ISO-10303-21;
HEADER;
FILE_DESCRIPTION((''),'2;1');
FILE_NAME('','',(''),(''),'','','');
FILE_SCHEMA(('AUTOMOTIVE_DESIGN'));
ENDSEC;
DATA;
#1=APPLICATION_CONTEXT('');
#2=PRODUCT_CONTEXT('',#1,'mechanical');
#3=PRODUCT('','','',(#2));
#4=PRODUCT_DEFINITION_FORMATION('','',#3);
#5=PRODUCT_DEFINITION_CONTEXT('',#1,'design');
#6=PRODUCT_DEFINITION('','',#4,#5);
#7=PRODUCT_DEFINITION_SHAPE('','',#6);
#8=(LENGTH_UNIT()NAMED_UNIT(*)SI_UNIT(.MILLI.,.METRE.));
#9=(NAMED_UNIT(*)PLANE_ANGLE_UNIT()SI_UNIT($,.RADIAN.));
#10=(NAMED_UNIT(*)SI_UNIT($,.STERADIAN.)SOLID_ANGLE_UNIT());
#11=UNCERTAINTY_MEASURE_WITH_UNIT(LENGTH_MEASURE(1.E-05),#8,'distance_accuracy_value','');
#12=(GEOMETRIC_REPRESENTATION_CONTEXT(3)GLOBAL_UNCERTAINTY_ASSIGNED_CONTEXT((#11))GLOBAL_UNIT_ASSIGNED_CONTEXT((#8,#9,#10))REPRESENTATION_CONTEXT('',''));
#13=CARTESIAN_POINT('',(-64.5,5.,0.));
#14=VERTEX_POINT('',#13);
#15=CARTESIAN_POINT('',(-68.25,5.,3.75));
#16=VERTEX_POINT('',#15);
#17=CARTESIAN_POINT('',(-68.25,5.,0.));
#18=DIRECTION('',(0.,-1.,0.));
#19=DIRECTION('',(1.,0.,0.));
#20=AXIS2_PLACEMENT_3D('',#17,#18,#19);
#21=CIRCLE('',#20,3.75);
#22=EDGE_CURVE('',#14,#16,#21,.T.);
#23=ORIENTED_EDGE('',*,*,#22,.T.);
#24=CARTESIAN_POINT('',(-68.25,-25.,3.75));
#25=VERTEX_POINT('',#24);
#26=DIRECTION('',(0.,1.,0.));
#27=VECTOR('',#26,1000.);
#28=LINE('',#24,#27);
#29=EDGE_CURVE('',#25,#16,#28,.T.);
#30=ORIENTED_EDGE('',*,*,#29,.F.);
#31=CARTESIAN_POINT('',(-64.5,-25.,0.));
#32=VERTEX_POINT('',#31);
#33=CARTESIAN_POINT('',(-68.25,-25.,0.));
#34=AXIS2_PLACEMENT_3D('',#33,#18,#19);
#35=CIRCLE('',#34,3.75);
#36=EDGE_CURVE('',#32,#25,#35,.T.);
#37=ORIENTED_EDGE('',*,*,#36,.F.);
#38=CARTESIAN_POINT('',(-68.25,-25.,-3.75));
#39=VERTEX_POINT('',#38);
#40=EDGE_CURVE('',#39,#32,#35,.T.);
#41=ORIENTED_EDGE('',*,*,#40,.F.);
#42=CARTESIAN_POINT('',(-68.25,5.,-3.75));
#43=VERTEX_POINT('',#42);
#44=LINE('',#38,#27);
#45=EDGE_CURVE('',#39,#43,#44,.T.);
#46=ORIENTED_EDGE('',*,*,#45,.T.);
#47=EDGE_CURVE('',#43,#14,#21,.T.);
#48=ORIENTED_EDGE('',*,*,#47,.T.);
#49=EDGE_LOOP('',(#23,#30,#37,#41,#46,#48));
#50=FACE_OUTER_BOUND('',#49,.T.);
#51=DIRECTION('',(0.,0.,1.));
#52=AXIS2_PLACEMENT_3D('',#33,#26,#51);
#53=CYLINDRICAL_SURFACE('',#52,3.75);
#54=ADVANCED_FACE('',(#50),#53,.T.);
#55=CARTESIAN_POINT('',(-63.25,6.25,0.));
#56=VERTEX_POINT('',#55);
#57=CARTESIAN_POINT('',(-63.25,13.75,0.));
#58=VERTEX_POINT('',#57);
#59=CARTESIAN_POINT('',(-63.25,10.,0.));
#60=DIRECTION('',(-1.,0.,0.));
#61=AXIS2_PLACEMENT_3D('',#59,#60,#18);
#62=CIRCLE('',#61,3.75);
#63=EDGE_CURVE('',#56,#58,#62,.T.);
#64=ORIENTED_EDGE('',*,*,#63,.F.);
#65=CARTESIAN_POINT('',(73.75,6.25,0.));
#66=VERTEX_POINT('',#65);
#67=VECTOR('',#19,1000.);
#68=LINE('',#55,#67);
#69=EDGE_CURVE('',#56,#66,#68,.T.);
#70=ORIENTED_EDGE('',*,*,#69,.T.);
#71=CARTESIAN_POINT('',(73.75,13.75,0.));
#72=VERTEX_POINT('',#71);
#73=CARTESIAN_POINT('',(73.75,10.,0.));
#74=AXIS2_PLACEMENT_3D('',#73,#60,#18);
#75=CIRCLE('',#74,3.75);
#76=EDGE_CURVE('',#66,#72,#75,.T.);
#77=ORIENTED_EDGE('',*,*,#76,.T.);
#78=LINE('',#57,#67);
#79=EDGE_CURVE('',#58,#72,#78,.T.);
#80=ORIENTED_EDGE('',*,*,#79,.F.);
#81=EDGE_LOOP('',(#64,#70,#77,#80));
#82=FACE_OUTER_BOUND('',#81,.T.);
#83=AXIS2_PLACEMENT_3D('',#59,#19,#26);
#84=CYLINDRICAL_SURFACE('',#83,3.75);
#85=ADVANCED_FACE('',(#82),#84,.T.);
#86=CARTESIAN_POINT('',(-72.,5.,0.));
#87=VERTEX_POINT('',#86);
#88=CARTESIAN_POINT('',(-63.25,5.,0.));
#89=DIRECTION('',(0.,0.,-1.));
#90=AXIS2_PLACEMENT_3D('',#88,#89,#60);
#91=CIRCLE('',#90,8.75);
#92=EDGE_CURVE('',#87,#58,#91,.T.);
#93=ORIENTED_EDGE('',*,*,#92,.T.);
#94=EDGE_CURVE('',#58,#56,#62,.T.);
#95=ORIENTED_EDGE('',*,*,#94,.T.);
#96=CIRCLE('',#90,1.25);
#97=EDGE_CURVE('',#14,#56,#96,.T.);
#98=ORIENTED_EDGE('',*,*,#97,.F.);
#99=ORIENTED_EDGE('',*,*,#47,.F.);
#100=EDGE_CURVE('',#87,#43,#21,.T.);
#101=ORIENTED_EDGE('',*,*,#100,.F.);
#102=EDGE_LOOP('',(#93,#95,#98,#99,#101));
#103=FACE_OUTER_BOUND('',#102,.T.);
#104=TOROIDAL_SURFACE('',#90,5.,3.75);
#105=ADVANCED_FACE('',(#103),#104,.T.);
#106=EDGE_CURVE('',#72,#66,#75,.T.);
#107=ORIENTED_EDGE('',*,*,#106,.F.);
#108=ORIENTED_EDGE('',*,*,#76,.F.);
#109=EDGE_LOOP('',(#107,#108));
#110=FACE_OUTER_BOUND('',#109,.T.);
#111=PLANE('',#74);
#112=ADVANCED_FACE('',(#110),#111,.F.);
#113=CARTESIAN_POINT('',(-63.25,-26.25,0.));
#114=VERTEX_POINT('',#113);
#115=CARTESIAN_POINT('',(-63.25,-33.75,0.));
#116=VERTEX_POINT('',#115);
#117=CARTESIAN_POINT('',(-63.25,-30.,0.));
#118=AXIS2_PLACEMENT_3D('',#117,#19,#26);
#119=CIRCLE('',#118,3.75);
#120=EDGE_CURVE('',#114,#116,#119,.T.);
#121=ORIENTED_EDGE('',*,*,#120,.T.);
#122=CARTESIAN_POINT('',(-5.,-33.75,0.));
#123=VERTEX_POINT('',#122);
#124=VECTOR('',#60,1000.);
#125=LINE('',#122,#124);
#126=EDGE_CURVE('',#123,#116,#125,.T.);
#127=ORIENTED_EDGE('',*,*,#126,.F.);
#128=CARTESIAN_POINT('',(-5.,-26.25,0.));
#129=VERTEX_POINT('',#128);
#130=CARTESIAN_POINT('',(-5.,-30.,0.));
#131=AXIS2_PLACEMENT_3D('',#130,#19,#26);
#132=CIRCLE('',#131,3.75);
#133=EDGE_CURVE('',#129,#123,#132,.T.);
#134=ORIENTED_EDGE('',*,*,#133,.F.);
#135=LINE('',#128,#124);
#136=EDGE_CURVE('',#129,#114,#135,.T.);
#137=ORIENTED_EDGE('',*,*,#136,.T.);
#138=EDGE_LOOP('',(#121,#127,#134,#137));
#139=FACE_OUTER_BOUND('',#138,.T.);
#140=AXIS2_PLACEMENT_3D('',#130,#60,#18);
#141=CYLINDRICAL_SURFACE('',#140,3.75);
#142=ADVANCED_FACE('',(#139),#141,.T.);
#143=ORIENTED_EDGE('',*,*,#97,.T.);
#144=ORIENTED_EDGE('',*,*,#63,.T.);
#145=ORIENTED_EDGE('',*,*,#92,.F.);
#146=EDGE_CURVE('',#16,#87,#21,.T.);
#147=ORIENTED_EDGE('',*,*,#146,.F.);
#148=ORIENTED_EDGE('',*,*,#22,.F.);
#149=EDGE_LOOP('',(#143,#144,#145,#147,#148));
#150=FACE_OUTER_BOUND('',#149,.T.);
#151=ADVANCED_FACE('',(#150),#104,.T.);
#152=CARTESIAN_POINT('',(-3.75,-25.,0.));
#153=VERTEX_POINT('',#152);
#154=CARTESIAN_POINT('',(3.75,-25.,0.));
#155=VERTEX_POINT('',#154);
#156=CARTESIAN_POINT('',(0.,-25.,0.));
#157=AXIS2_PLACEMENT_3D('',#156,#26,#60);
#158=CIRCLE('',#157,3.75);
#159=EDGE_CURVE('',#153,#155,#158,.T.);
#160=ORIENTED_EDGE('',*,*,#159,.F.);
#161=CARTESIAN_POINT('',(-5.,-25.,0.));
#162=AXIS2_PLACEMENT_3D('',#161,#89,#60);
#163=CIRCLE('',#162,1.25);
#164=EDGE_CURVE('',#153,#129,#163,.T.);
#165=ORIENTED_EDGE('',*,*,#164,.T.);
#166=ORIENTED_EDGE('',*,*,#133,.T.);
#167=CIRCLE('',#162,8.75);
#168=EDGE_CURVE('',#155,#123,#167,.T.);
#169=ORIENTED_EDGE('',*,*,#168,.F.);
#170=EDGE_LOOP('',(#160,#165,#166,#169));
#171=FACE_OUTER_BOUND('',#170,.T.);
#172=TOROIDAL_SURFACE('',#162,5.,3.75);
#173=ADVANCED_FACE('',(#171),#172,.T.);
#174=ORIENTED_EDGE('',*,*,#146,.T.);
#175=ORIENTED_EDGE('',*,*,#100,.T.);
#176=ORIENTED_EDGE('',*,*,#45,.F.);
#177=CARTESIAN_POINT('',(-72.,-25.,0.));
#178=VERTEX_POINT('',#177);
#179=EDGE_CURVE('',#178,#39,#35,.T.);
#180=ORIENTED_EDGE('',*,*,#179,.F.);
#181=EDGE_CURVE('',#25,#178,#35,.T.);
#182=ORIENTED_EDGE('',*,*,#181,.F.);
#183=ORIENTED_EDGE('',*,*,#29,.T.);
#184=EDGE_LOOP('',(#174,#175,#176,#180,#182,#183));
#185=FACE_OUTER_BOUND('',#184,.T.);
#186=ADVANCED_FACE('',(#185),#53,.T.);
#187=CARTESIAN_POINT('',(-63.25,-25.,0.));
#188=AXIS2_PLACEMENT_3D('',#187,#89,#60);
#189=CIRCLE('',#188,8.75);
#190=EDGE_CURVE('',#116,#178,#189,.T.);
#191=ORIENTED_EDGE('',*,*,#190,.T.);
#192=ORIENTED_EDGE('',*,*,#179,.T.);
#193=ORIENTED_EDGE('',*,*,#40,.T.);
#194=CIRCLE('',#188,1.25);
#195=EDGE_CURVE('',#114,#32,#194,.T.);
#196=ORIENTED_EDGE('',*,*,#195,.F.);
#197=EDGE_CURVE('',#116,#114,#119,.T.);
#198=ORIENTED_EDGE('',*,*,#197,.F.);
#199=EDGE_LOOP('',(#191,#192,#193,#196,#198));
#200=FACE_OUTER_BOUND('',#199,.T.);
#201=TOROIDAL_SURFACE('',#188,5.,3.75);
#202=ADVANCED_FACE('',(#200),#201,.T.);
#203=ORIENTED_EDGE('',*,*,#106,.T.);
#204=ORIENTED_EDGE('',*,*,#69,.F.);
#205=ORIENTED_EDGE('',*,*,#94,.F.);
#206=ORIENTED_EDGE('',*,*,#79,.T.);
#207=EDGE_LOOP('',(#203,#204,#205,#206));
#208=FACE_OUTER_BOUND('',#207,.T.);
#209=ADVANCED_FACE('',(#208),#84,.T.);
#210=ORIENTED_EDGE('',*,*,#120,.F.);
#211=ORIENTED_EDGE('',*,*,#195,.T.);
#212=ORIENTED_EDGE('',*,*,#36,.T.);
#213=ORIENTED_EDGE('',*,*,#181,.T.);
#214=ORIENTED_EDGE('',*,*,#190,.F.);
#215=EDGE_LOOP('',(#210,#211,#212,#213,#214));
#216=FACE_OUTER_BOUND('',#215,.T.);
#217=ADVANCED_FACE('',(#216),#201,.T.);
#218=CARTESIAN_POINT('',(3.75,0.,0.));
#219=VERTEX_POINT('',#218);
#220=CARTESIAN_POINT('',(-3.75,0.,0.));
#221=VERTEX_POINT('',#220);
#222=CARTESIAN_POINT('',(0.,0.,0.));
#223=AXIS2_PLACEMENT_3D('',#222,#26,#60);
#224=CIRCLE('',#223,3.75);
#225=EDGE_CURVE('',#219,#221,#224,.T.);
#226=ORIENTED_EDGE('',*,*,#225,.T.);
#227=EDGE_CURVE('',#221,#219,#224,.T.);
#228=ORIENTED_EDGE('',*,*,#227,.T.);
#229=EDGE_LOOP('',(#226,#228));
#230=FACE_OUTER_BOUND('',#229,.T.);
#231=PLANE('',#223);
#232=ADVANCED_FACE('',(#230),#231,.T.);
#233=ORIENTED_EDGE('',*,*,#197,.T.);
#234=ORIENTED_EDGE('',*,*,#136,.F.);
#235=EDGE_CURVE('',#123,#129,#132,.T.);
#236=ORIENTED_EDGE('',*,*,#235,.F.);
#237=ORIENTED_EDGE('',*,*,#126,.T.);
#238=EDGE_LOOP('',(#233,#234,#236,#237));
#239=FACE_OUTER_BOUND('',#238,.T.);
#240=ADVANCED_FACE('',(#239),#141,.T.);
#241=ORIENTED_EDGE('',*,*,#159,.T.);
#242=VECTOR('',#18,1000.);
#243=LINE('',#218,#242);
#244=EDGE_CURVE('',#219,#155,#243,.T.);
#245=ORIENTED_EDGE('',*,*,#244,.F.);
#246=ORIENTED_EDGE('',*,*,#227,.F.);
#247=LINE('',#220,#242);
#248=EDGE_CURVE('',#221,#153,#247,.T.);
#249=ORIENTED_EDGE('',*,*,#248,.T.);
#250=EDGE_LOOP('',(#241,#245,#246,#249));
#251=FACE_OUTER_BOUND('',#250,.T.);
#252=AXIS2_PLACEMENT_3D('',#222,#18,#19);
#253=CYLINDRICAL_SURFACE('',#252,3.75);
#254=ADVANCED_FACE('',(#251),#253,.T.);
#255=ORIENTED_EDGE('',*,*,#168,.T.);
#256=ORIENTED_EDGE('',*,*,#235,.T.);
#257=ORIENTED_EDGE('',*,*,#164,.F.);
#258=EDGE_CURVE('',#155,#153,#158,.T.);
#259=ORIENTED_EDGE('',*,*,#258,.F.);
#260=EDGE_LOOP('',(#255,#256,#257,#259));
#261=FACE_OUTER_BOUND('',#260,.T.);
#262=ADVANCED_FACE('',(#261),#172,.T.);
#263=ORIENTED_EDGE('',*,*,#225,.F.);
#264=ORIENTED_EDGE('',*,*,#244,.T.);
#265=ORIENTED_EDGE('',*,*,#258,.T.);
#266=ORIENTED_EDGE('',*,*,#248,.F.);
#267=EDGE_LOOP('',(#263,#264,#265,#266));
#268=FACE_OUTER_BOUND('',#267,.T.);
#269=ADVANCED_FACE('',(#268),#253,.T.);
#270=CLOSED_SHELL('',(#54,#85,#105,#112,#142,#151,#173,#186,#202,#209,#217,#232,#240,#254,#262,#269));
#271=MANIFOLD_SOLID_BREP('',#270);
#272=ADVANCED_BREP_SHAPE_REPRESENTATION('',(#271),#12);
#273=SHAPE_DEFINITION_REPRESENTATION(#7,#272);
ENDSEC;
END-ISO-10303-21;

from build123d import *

# Parameters (mm, degrees)
BOLT_ROD_SWEEP_7_5_PROFILE_R = 3.75


with BuildPart() as part:
    # Bolt Rod Sweep Ø7.5: sweep along a path in Bolt Rod Path
    with BuildLine(Plane.XY) as bolt_rod_sweep_7_5_path:
        Line((0, 0), (0, -25))
        ThreePointArc((0, -25), (-1.464466094, -28.535533906), (-5, -30))
        Line((-5, -30), (-63.25, -30))
        ThreePointArc((-63.25, -30), (-66.785533906, -28.535533906), (-68.25, -25))
        Line((-68.25, -25), (-68.25, 5))
        ThreePointArc((-68.25, 5), (-66.785533906, 8.535533906), (-63.25, 10))
        Line((-63.25, 10), (73.75, 10))
    # Bolt Rod Sweep Ø7.5 profile (on start of the path) → Bolt Rod Sweep Ø7.5 (sweep)
    with BuildSketch(Plane(origin=(0, 0, 0), x_dir=(-1, 0, 0), z_dir=(0, -1, 0))):
        Circle(BOLT_ROD_SWEEP_7_5_PROFILE_R)
    sweep(path=bolt_rod_sweep_7_5_path.line)


solid = part.part
